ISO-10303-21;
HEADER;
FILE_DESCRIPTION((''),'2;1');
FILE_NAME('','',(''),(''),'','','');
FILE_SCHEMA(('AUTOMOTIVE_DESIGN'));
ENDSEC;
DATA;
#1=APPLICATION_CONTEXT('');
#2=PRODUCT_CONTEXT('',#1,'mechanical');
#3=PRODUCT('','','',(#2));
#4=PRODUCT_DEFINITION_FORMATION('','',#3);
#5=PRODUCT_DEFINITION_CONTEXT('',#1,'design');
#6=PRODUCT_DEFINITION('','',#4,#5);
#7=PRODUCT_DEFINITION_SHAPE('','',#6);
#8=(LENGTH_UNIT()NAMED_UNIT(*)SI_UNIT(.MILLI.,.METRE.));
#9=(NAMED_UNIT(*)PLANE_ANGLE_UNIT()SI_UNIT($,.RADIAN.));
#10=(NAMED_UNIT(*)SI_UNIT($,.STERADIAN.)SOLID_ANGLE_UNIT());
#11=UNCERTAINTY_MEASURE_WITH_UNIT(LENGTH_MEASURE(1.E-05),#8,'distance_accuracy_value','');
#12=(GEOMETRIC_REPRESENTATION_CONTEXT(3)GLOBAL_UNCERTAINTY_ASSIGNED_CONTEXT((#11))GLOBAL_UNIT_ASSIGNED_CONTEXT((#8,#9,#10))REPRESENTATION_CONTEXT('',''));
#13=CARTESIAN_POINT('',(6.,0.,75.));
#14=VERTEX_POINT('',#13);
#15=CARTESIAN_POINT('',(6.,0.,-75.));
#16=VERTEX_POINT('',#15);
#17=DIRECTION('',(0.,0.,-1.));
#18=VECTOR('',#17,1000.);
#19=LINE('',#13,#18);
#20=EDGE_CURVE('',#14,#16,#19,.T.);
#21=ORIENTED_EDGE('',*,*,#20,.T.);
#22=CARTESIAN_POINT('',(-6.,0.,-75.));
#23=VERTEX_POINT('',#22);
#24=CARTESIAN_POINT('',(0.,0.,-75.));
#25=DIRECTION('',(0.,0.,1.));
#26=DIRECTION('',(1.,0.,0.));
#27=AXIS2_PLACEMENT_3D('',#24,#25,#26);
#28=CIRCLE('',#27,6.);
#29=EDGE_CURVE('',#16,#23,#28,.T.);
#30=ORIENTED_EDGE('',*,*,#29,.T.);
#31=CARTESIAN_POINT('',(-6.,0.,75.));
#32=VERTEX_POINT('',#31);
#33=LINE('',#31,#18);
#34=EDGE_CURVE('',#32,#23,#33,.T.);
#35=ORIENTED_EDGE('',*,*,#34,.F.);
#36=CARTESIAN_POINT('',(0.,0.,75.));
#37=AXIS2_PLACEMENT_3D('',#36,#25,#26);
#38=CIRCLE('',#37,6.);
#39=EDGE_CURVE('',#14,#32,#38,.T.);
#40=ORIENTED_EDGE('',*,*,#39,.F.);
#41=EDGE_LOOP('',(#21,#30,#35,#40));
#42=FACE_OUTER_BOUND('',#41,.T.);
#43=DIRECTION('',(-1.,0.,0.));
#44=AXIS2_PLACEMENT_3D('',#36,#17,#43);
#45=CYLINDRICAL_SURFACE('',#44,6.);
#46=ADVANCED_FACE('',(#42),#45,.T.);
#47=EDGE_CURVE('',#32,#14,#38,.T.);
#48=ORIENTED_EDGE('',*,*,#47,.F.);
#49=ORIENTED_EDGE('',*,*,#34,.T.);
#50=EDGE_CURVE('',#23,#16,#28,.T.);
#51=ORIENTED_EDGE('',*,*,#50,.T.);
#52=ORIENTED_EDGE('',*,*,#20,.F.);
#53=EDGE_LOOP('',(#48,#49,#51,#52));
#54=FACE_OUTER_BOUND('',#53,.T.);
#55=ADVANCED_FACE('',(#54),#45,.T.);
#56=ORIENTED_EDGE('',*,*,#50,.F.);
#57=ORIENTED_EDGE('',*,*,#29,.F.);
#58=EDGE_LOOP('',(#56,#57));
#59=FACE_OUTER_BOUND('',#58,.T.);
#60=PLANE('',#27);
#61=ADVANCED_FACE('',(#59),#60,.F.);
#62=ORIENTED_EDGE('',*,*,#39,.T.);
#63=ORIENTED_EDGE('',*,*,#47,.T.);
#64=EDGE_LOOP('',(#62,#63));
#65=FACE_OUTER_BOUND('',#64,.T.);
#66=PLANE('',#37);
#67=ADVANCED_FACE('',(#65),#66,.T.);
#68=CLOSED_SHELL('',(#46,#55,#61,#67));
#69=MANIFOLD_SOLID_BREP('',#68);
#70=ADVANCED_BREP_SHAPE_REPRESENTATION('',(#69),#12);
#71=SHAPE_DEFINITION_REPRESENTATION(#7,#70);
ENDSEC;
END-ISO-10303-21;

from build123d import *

# Parameters (mm, degrees)
SKETCH_1_R      = 6
EXTRUDE_1_DEPTH = 75


with BuildPart() as part:
    # 草图1 → 凸台-拉伸1 (new, symmetric)
    with BuildSketch(Plane.XY):
        Circle(SKETCH_1_R)
    extrude(amount=EXTRUDE_1_DEPTH, both=True)


solid = part.part
